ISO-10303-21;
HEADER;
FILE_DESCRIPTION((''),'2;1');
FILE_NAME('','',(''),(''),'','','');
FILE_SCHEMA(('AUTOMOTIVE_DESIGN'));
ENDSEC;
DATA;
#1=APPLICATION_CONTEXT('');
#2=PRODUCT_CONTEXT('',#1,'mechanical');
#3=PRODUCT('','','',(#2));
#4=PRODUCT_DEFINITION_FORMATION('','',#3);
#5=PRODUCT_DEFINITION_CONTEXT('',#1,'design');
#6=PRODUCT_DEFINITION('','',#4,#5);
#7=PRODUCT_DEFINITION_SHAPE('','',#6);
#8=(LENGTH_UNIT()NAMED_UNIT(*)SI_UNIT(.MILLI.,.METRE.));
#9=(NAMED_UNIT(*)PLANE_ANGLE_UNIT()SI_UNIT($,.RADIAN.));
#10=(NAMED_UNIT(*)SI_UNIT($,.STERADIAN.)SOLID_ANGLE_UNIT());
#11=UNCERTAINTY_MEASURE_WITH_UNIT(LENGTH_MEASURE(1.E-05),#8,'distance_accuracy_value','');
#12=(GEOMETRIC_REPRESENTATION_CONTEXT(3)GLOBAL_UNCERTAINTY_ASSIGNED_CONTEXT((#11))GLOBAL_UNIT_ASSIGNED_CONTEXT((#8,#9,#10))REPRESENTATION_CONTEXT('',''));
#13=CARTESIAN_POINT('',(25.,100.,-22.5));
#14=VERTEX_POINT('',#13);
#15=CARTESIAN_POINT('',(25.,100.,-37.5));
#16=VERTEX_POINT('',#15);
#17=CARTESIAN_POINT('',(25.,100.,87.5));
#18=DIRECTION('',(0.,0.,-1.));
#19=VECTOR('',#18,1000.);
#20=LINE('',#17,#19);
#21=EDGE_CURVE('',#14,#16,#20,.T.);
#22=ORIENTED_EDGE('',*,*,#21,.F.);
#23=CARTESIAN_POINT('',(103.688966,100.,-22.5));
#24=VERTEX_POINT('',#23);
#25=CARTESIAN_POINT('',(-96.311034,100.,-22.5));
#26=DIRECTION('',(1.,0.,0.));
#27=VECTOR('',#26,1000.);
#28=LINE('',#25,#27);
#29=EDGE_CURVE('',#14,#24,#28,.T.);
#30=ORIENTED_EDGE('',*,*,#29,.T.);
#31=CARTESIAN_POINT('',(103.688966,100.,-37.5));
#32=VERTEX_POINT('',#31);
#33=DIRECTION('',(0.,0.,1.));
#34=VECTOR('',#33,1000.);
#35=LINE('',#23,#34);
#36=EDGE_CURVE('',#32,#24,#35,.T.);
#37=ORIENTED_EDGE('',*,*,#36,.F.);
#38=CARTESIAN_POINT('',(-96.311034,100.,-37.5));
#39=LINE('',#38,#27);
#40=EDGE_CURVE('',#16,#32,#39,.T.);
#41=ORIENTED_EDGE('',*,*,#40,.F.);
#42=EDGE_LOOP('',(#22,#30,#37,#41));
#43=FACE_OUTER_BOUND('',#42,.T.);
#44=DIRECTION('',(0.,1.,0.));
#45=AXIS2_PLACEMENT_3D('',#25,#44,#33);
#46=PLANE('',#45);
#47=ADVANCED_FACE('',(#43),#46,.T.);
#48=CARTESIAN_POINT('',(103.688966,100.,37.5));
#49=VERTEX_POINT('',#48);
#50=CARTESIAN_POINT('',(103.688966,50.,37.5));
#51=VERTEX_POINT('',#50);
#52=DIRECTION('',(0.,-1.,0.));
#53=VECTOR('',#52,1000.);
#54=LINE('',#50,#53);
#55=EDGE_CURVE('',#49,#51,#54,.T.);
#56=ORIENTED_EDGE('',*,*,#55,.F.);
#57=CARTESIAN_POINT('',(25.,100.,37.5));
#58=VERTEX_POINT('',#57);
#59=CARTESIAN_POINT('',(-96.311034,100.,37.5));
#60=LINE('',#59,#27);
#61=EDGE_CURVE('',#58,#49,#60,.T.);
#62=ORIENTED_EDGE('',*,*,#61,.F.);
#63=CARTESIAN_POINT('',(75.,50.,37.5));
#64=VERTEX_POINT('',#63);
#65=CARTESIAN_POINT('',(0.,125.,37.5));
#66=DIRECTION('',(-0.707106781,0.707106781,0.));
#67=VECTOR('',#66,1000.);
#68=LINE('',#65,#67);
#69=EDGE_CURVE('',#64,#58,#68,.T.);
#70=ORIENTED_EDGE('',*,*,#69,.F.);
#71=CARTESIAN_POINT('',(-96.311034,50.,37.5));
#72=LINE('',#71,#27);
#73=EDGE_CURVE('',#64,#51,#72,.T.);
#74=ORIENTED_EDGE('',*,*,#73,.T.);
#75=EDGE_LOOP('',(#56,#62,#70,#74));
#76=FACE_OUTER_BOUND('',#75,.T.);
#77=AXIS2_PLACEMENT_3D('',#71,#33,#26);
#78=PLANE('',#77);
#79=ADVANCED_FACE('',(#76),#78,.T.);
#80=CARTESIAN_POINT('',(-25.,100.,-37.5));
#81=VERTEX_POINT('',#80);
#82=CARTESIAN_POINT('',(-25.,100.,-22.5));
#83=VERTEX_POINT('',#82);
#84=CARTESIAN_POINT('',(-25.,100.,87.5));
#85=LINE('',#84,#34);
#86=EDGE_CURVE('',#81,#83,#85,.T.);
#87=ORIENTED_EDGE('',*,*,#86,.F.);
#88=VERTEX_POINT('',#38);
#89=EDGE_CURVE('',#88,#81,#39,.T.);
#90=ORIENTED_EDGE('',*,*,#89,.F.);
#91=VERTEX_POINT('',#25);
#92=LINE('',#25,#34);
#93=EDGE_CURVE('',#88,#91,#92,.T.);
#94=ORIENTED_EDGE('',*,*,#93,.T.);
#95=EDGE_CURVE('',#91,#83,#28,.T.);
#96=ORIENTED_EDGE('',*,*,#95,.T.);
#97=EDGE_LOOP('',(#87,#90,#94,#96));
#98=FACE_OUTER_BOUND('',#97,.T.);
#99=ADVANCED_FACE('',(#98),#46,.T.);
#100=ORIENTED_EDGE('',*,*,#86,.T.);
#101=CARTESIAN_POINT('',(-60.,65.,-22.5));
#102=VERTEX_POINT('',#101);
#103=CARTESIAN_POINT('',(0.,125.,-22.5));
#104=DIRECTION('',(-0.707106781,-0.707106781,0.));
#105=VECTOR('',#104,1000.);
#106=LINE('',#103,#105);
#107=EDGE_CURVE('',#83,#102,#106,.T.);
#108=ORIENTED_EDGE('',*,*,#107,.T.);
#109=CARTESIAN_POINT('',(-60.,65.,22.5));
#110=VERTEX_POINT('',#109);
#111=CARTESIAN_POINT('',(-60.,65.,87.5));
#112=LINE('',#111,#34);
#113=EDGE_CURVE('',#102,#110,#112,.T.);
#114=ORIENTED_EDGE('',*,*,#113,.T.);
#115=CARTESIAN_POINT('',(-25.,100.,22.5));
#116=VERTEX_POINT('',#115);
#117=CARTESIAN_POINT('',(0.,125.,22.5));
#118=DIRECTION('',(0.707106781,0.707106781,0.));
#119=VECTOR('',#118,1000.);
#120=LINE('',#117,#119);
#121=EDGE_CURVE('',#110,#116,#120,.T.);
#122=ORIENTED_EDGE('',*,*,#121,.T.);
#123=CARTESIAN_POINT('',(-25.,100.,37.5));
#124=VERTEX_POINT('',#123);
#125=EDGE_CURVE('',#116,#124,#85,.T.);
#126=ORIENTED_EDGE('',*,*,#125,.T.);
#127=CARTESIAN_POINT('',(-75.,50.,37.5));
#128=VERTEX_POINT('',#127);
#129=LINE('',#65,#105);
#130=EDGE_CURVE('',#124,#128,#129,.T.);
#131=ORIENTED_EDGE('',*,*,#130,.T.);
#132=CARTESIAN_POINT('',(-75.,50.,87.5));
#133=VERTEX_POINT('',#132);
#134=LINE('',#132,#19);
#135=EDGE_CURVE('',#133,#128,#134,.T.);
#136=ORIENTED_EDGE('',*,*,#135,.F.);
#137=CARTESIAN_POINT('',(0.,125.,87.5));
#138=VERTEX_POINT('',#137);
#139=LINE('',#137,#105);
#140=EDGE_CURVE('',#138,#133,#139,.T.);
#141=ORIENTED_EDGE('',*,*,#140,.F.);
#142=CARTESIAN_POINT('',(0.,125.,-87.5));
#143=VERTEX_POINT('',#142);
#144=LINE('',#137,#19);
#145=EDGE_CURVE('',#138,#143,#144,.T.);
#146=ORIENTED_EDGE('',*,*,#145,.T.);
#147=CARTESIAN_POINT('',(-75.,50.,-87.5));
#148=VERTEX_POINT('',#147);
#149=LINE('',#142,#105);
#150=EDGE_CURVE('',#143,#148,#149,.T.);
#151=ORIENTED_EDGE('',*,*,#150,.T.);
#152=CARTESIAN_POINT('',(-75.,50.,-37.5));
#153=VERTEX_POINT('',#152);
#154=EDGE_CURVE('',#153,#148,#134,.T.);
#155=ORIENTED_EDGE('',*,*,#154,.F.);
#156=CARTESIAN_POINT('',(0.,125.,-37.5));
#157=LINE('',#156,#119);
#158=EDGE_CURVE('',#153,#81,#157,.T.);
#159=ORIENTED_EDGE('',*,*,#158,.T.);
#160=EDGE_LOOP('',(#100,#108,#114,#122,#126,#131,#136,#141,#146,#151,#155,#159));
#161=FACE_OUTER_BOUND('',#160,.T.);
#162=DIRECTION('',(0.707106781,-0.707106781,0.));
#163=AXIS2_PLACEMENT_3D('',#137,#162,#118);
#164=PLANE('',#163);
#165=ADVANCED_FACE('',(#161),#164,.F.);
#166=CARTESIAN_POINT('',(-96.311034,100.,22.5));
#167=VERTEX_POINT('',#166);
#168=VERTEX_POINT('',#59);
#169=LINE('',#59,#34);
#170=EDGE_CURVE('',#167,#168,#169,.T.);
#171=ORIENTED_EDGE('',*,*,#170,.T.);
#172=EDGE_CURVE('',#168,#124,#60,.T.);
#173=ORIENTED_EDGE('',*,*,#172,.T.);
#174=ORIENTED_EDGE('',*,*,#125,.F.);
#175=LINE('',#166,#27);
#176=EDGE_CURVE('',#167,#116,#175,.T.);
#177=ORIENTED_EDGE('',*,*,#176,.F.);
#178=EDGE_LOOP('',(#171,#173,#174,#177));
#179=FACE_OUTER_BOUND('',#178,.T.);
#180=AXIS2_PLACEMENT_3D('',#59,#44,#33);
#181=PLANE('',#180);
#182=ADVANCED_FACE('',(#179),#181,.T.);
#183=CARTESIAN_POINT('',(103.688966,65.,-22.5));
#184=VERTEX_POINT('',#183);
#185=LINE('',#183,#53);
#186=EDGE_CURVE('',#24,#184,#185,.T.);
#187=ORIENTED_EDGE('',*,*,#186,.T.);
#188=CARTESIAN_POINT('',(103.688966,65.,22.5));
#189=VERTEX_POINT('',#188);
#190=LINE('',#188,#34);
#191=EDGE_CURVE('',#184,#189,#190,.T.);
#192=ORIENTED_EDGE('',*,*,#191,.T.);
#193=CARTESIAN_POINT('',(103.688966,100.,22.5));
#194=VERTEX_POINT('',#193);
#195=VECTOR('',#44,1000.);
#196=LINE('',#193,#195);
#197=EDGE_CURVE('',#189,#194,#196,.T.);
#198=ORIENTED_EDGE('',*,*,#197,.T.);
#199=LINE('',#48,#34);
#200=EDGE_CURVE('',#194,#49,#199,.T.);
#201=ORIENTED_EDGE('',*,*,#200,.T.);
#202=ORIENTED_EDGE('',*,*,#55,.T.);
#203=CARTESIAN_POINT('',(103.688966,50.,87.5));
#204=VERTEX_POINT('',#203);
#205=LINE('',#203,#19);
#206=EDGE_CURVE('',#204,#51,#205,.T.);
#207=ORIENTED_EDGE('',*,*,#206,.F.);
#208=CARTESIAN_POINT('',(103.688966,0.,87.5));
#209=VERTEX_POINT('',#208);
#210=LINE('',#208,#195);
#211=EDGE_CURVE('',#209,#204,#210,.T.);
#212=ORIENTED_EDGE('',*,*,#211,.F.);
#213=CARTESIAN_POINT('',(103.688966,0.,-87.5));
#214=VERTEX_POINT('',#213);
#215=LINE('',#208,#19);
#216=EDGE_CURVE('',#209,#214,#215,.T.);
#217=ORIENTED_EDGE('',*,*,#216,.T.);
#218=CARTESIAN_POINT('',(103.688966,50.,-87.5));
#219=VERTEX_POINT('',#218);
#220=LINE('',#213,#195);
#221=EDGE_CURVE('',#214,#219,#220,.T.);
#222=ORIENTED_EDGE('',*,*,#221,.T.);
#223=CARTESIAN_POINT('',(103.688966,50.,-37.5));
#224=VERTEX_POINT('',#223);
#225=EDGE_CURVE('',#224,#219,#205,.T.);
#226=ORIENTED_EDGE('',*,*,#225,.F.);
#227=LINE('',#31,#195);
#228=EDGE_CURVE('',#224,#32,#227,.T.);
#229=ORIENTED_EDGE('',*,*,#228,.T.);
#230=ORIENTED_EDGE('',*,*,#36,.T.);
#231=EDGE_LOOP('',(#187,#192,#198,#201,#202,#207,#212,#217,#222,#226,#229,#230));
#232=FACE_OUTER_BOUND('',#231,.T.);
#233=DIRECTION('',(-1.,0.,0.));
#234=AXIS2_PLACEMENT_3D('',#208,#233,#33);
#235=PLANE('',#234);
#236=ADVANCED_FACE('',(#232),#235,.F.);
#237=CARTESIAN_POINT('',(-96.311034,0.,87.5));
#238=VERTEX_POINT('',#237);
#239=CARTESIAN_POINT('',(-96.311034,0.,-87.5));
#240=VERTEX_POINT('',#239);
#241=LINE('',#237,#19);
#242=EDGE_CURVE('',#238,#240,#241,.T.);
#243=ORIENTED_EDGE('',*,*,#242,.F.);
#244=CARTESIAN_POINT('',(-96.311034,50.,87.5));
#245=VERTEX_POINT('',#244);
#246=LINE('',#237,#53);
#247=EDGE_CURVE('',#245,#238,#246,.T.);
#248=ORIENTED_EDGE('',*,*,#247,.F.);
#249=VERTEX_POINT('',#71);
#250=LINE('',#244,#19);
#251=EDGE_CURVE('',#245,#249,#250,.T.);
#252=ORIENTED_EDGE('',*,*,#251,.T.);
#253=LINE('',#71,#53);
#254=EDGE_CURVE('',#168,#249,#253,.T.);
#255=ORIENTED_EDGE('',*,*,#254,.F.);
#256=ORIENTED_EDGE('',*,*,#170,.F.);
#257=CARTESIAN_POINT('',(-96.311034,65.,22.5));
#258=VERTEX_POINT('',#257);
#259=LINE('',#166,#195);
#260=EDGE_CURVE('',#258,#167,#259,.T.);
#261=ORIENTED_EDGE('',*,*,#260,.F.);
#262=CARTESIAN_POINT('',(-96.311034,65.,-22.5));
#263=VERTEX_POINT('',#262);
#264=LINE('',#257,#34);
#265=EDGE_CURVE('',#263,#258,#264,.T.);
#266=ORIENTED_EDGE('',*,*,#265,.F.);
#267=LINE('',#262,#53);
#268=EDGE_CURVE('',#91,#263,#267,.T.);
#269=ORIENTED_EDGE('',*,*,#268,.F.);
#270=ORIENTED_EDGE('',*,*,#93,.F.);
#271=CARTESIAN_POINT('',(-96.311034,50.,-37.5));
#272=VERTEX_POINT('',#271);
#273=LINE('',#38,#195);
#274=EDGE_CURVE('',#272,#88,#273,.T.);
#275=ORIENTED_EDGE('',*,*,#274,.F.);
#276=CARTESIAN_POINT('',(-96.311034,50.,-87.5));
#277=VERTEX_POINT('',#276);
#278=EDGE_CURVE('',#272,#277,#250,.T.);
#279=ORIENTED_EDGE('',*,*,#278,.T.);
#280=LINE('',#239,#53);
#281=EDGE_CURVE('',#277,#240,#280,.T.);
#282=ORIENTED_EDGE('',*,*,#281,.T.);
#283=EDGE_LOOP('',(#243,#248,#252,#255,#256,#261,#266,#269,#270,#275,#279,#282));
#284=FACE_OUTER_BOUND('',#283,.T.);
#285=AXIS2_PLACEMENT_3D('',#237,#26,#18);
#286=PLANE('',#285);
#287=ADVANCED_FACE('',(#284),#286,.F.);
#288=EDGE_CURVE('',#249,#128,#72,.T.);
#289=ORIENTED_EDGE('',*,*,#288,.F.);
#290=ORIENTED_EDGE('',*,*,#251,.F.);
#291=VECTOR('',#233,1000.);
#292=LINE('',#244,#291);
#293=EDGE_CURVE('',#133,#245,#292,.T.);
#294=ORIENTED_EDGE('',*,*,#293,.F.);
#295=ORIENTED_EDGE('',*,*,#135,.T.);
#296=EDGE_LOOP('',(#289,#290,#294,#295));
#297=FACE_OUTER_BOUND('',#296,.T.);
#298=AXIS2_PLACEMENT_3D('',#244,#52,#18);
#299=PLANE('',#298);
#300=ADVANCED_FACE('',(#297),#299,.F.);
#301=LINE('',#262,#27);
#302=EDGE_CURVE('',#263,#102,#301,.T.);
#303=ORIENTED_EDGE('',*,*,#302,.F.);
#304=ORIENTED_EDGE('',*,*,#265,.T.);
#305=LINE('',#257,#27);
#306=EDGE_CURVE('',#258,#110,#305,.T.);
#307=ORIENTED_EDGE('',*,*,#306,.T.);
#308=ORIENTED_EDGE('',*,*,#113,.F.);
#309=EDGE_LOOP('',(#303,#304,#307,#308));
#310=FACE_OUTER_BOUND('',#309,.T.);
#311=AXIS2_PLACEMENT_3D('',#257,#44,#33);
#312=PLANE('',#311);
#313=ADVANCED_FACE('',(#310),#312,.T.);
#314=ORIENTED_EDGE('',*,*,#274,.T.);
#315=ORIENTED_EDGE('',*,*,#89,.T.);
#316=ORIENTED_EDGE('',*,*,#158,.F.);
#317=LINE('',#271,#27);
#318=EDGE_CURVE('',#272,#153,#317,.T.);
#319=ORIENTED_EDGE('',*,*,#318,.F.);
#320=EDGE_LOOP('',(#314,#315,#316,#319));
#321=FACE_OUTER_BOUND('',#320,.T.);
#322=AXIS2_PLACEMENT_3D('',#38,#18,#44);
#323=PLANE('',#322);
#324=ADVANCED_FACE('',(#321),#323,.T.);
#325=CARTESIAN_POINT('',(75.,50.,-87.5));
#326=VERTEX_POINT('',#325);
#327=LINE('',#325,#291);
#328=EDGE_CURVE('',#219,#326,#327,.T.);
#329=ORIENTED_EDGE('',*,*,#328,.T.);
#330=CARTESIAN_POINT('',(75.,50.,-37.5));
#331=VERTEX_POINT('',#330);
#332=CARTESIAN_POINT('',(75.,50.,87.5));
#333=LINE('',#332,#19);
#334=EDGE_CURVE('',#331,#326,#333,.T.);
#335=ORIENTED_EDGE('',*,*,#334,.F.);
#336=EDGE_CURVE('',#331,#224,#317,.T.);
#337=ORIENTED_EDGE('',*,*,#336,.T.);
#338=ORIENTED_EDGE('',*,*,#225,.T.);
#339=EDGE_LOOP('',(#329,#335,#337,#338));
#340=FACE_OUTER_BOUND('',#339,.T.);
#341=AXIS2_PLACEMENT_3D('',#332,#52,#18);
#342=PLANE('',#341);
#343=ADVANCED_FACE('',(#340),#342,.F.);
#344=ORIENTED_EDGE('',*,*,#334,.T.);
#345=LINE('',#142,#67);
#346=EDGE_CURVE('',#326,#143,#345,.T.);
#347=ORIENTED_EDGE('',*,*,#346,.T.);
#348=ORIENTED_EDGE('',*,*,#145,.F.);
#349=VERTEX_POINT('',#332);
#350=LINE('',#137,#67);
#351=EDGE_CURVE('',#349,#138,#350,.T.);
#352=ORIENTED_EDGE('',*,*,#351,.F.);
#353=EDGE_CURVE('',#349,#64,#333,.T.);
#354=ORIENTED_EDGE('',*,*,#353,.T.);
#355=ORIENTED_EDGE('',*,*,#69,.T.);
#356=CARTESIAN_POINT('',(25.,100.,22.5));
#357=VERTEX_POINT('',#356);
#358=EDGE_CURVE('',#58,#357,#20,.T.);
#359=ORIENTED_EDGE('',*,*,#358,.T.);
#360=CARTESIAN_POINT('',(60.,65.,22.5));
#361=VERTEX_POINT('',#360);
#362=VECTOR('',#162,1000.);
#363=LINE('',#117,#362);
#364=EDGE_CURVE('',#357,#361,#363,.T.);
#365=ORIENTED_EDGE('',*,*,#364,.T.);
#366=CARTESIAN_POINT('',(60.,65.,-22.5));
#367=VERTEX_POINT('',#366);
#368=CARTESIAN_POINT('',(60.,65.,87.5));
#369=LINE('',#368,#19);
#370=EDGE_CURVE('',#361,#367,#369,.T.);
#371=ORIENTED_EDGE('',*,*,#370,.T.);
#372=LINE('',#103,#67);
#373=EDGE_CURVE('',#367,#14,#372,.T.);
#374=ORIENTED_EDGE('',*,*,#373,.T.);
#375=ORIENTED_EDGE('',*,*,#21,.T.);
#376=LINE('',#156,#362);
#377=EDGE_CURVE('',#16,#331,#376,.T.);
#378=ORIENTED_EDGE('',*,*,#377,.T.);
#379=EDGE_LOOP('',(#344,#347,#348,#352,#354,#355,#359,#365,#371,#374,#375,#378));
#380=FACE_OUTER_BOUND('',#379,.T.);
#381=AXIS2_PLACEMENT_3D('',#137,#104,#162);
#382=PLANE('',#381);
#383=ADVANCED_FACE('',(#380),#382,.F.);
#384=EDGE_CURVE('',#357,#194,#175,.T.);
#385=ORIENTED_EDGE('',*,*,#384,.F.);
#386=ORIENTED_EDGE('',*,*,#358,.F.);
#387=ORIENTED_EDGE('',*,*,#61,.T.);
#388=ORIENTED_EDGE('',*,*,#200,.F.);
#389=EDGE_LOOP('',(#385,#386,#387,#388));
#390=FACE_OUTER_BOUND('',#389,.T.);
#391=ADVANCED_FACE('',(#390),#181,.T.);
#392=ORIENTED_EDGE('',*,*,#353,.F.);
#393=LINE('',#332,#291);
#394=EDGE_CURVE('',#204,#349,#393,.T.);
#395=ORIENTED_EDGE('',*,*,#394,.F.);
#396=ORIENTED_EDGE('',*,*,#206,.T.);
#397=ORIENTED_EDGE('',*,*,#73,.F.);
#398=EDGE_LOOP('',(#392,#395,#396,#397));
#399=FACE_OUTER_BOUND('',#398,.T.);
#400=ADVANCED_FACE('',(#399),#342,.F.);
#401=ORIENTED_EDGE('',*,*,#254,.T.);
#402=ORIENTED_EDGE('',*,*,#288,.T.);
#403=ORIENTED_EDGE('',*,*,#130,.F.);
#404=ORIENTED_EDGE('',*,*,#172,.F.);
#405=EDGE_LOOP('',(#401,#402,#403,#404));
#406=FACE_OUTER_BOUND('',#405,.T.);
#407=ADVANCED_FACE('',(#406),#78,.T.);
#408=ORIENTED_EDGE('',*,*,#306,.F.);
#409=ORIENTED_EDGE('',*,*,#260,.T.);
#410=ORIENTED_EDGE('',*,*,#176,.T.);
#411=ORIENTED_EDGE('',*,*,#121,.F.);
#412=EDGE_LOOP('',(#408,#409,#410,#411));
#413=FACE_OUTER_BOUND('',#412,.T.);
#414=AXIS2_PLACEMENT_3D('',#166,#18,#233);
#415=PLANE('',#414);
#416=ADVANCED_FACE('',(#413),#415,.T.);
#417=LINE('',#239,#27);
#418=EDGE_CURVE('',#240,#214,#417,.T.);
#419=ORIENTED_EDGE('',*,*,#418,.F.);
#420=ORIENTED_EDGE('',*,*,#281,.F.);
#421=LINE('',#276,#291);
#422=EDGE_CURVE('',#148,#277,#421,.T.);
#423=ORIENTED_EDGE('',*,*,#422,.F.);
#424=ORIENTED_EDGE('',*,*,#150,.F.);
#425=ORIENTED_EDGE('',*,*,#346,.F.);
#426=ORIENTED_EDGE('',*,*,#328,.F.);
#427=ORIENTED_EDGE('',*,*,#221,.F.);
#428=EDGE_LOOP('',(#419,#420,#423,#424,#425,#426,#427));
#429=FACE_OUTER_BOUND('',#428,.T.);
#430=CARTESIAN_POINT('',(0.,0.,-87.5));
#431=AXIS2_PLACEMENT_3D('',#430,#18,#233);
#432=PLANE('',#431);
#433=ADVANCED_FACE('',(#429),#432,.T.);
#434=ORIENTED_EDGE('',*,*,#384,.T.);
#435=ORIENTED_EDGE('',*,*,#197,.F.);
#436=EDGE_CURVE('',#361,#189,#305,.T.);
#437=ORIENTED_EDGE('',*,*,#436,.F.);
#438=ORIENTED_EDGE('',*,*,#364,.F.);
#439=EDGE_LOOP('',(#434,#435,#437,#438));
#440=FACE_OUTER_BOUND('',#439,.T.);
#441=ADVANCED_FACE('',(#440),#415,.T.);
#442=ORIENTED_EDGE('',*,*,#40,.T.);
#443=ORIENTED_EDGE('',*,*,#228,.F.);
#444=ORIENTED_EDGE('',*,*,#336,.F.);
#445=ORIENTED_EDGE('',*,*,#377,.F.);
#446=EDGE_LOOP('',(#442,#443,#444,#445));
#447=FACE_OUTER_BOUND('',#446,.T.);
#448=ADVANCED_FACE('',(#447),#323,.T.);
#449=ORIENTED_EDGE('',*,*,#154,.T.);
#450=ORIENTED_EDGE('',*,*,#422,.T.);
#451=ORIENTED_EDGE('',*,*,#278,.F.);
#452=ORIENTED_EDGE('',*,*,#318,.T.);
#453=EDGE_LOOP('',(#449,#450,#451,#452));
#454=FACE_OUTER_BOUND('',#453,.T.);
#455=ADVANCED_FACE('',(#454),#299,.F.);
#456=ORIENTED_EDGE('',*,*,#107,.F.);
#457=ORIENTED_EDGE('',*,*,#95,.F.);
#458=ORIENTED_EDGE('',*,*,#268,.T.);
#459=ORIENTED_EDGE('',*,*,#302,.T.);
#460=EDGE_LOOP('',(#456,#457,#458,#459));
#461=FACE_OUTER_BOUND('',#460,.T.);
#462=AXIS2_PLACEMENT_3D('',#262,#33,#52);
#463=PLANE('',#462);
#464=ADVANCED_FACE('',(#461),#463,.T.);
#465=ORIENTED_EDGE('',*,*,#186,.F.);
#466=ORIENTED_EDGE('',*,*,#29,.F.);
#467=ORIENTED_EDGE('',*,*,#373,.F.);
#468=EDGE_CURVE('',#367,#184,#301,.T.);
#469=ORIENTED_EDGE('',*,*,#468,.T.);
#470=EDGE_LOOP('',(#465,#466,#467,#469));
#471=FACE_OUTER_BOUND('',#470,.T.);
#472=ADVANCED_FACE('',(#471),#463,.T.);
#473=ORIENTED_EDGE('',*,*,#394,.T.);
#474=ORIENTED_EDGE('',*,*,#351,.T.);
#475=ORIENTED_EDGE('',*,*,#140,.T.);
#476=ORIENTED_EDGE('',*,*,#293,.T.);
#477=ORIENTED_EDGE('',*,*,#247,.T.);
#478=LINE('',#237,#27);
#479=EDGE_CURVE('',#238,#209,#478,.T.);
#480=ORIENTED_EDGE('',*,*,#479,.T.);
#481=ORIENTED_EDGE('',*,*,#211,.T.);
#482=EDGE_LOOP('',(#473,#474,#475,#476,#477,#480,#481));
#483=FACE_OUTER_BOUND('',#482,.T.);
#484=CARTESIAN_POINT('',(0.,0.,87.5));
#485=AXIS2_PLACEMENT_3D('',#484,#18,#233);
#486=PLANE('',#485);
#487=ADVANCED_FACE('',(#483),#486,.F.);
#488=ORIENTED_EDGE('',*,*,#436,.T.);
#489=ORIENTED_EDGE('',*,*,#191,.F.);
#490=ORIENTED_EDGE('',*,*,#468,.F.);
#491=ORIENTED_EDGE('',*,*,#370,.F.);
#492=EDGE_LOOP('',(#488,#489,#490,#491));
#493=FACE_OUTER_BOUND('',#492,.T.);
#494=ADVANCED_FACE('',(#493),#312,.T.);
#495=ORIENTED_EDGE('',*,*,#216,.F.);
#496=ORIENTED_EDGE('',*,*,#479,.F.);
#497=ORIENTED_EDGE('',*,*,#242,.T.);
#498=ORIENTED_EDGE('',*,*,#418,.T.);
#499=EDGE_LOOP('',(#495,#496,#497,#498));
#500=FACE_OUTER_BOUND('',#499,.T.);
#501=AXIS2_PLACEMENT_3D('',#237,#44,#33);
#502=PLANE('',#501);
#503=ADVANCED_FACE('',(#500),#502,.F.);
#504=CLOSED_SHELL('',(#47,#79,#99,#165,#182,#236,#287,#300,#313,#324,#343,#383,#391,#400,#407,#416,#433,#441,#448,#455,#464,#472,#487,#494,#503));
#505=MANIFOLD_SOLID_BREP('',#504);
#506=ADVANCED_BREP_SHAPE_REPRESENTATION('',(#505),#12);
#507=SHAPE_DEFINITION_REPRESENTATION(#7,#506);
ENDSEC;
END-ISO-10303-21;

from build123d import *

# Parameters (mm, degrees)
BASE_WEDGE_BLOCK_DEPTH = 87.5
TWIN_START             = -200
TWIN_SLOTS_15MM_DEPTH  = 200


with BuildPart() as part:
    # Base Profile Sketch → Base Wedge Block (new, symmetric)
    with BuildSketch(Plane.XY):
        Polygon((-96.311034199, 0), (103.688965801, 0), (103.688965801, 50), (75, 50), (0, 125), (-75, 50), (-96.311034199, 50), align=None)
    extrude(amount=BASE_WEDGE_BLOCK_DEPTH, both=True)

    # Slot Profile Sketch → Twin Slots 15mm (add)
    with BuildSketch(Plane(origin=(103.688965801, 0, 0), x_dir=(0, 0, -1), z_dir=(1, 0, 0)).offset(TWIN_START)):
        Polygon((-87.5, 0), (-87.5, 50), (-37.5, 50), (-37.5, 100), (-22.5, 100), (-22.5, 65), (22.5, 65), (22.5, 100), (37.5, 100), (37.5, 50), (87.5, 50), (87.5, 0), align=None)
    extrude(amount=TWIN_SLOTS_15MM_DEPTH)


solid = part.part
